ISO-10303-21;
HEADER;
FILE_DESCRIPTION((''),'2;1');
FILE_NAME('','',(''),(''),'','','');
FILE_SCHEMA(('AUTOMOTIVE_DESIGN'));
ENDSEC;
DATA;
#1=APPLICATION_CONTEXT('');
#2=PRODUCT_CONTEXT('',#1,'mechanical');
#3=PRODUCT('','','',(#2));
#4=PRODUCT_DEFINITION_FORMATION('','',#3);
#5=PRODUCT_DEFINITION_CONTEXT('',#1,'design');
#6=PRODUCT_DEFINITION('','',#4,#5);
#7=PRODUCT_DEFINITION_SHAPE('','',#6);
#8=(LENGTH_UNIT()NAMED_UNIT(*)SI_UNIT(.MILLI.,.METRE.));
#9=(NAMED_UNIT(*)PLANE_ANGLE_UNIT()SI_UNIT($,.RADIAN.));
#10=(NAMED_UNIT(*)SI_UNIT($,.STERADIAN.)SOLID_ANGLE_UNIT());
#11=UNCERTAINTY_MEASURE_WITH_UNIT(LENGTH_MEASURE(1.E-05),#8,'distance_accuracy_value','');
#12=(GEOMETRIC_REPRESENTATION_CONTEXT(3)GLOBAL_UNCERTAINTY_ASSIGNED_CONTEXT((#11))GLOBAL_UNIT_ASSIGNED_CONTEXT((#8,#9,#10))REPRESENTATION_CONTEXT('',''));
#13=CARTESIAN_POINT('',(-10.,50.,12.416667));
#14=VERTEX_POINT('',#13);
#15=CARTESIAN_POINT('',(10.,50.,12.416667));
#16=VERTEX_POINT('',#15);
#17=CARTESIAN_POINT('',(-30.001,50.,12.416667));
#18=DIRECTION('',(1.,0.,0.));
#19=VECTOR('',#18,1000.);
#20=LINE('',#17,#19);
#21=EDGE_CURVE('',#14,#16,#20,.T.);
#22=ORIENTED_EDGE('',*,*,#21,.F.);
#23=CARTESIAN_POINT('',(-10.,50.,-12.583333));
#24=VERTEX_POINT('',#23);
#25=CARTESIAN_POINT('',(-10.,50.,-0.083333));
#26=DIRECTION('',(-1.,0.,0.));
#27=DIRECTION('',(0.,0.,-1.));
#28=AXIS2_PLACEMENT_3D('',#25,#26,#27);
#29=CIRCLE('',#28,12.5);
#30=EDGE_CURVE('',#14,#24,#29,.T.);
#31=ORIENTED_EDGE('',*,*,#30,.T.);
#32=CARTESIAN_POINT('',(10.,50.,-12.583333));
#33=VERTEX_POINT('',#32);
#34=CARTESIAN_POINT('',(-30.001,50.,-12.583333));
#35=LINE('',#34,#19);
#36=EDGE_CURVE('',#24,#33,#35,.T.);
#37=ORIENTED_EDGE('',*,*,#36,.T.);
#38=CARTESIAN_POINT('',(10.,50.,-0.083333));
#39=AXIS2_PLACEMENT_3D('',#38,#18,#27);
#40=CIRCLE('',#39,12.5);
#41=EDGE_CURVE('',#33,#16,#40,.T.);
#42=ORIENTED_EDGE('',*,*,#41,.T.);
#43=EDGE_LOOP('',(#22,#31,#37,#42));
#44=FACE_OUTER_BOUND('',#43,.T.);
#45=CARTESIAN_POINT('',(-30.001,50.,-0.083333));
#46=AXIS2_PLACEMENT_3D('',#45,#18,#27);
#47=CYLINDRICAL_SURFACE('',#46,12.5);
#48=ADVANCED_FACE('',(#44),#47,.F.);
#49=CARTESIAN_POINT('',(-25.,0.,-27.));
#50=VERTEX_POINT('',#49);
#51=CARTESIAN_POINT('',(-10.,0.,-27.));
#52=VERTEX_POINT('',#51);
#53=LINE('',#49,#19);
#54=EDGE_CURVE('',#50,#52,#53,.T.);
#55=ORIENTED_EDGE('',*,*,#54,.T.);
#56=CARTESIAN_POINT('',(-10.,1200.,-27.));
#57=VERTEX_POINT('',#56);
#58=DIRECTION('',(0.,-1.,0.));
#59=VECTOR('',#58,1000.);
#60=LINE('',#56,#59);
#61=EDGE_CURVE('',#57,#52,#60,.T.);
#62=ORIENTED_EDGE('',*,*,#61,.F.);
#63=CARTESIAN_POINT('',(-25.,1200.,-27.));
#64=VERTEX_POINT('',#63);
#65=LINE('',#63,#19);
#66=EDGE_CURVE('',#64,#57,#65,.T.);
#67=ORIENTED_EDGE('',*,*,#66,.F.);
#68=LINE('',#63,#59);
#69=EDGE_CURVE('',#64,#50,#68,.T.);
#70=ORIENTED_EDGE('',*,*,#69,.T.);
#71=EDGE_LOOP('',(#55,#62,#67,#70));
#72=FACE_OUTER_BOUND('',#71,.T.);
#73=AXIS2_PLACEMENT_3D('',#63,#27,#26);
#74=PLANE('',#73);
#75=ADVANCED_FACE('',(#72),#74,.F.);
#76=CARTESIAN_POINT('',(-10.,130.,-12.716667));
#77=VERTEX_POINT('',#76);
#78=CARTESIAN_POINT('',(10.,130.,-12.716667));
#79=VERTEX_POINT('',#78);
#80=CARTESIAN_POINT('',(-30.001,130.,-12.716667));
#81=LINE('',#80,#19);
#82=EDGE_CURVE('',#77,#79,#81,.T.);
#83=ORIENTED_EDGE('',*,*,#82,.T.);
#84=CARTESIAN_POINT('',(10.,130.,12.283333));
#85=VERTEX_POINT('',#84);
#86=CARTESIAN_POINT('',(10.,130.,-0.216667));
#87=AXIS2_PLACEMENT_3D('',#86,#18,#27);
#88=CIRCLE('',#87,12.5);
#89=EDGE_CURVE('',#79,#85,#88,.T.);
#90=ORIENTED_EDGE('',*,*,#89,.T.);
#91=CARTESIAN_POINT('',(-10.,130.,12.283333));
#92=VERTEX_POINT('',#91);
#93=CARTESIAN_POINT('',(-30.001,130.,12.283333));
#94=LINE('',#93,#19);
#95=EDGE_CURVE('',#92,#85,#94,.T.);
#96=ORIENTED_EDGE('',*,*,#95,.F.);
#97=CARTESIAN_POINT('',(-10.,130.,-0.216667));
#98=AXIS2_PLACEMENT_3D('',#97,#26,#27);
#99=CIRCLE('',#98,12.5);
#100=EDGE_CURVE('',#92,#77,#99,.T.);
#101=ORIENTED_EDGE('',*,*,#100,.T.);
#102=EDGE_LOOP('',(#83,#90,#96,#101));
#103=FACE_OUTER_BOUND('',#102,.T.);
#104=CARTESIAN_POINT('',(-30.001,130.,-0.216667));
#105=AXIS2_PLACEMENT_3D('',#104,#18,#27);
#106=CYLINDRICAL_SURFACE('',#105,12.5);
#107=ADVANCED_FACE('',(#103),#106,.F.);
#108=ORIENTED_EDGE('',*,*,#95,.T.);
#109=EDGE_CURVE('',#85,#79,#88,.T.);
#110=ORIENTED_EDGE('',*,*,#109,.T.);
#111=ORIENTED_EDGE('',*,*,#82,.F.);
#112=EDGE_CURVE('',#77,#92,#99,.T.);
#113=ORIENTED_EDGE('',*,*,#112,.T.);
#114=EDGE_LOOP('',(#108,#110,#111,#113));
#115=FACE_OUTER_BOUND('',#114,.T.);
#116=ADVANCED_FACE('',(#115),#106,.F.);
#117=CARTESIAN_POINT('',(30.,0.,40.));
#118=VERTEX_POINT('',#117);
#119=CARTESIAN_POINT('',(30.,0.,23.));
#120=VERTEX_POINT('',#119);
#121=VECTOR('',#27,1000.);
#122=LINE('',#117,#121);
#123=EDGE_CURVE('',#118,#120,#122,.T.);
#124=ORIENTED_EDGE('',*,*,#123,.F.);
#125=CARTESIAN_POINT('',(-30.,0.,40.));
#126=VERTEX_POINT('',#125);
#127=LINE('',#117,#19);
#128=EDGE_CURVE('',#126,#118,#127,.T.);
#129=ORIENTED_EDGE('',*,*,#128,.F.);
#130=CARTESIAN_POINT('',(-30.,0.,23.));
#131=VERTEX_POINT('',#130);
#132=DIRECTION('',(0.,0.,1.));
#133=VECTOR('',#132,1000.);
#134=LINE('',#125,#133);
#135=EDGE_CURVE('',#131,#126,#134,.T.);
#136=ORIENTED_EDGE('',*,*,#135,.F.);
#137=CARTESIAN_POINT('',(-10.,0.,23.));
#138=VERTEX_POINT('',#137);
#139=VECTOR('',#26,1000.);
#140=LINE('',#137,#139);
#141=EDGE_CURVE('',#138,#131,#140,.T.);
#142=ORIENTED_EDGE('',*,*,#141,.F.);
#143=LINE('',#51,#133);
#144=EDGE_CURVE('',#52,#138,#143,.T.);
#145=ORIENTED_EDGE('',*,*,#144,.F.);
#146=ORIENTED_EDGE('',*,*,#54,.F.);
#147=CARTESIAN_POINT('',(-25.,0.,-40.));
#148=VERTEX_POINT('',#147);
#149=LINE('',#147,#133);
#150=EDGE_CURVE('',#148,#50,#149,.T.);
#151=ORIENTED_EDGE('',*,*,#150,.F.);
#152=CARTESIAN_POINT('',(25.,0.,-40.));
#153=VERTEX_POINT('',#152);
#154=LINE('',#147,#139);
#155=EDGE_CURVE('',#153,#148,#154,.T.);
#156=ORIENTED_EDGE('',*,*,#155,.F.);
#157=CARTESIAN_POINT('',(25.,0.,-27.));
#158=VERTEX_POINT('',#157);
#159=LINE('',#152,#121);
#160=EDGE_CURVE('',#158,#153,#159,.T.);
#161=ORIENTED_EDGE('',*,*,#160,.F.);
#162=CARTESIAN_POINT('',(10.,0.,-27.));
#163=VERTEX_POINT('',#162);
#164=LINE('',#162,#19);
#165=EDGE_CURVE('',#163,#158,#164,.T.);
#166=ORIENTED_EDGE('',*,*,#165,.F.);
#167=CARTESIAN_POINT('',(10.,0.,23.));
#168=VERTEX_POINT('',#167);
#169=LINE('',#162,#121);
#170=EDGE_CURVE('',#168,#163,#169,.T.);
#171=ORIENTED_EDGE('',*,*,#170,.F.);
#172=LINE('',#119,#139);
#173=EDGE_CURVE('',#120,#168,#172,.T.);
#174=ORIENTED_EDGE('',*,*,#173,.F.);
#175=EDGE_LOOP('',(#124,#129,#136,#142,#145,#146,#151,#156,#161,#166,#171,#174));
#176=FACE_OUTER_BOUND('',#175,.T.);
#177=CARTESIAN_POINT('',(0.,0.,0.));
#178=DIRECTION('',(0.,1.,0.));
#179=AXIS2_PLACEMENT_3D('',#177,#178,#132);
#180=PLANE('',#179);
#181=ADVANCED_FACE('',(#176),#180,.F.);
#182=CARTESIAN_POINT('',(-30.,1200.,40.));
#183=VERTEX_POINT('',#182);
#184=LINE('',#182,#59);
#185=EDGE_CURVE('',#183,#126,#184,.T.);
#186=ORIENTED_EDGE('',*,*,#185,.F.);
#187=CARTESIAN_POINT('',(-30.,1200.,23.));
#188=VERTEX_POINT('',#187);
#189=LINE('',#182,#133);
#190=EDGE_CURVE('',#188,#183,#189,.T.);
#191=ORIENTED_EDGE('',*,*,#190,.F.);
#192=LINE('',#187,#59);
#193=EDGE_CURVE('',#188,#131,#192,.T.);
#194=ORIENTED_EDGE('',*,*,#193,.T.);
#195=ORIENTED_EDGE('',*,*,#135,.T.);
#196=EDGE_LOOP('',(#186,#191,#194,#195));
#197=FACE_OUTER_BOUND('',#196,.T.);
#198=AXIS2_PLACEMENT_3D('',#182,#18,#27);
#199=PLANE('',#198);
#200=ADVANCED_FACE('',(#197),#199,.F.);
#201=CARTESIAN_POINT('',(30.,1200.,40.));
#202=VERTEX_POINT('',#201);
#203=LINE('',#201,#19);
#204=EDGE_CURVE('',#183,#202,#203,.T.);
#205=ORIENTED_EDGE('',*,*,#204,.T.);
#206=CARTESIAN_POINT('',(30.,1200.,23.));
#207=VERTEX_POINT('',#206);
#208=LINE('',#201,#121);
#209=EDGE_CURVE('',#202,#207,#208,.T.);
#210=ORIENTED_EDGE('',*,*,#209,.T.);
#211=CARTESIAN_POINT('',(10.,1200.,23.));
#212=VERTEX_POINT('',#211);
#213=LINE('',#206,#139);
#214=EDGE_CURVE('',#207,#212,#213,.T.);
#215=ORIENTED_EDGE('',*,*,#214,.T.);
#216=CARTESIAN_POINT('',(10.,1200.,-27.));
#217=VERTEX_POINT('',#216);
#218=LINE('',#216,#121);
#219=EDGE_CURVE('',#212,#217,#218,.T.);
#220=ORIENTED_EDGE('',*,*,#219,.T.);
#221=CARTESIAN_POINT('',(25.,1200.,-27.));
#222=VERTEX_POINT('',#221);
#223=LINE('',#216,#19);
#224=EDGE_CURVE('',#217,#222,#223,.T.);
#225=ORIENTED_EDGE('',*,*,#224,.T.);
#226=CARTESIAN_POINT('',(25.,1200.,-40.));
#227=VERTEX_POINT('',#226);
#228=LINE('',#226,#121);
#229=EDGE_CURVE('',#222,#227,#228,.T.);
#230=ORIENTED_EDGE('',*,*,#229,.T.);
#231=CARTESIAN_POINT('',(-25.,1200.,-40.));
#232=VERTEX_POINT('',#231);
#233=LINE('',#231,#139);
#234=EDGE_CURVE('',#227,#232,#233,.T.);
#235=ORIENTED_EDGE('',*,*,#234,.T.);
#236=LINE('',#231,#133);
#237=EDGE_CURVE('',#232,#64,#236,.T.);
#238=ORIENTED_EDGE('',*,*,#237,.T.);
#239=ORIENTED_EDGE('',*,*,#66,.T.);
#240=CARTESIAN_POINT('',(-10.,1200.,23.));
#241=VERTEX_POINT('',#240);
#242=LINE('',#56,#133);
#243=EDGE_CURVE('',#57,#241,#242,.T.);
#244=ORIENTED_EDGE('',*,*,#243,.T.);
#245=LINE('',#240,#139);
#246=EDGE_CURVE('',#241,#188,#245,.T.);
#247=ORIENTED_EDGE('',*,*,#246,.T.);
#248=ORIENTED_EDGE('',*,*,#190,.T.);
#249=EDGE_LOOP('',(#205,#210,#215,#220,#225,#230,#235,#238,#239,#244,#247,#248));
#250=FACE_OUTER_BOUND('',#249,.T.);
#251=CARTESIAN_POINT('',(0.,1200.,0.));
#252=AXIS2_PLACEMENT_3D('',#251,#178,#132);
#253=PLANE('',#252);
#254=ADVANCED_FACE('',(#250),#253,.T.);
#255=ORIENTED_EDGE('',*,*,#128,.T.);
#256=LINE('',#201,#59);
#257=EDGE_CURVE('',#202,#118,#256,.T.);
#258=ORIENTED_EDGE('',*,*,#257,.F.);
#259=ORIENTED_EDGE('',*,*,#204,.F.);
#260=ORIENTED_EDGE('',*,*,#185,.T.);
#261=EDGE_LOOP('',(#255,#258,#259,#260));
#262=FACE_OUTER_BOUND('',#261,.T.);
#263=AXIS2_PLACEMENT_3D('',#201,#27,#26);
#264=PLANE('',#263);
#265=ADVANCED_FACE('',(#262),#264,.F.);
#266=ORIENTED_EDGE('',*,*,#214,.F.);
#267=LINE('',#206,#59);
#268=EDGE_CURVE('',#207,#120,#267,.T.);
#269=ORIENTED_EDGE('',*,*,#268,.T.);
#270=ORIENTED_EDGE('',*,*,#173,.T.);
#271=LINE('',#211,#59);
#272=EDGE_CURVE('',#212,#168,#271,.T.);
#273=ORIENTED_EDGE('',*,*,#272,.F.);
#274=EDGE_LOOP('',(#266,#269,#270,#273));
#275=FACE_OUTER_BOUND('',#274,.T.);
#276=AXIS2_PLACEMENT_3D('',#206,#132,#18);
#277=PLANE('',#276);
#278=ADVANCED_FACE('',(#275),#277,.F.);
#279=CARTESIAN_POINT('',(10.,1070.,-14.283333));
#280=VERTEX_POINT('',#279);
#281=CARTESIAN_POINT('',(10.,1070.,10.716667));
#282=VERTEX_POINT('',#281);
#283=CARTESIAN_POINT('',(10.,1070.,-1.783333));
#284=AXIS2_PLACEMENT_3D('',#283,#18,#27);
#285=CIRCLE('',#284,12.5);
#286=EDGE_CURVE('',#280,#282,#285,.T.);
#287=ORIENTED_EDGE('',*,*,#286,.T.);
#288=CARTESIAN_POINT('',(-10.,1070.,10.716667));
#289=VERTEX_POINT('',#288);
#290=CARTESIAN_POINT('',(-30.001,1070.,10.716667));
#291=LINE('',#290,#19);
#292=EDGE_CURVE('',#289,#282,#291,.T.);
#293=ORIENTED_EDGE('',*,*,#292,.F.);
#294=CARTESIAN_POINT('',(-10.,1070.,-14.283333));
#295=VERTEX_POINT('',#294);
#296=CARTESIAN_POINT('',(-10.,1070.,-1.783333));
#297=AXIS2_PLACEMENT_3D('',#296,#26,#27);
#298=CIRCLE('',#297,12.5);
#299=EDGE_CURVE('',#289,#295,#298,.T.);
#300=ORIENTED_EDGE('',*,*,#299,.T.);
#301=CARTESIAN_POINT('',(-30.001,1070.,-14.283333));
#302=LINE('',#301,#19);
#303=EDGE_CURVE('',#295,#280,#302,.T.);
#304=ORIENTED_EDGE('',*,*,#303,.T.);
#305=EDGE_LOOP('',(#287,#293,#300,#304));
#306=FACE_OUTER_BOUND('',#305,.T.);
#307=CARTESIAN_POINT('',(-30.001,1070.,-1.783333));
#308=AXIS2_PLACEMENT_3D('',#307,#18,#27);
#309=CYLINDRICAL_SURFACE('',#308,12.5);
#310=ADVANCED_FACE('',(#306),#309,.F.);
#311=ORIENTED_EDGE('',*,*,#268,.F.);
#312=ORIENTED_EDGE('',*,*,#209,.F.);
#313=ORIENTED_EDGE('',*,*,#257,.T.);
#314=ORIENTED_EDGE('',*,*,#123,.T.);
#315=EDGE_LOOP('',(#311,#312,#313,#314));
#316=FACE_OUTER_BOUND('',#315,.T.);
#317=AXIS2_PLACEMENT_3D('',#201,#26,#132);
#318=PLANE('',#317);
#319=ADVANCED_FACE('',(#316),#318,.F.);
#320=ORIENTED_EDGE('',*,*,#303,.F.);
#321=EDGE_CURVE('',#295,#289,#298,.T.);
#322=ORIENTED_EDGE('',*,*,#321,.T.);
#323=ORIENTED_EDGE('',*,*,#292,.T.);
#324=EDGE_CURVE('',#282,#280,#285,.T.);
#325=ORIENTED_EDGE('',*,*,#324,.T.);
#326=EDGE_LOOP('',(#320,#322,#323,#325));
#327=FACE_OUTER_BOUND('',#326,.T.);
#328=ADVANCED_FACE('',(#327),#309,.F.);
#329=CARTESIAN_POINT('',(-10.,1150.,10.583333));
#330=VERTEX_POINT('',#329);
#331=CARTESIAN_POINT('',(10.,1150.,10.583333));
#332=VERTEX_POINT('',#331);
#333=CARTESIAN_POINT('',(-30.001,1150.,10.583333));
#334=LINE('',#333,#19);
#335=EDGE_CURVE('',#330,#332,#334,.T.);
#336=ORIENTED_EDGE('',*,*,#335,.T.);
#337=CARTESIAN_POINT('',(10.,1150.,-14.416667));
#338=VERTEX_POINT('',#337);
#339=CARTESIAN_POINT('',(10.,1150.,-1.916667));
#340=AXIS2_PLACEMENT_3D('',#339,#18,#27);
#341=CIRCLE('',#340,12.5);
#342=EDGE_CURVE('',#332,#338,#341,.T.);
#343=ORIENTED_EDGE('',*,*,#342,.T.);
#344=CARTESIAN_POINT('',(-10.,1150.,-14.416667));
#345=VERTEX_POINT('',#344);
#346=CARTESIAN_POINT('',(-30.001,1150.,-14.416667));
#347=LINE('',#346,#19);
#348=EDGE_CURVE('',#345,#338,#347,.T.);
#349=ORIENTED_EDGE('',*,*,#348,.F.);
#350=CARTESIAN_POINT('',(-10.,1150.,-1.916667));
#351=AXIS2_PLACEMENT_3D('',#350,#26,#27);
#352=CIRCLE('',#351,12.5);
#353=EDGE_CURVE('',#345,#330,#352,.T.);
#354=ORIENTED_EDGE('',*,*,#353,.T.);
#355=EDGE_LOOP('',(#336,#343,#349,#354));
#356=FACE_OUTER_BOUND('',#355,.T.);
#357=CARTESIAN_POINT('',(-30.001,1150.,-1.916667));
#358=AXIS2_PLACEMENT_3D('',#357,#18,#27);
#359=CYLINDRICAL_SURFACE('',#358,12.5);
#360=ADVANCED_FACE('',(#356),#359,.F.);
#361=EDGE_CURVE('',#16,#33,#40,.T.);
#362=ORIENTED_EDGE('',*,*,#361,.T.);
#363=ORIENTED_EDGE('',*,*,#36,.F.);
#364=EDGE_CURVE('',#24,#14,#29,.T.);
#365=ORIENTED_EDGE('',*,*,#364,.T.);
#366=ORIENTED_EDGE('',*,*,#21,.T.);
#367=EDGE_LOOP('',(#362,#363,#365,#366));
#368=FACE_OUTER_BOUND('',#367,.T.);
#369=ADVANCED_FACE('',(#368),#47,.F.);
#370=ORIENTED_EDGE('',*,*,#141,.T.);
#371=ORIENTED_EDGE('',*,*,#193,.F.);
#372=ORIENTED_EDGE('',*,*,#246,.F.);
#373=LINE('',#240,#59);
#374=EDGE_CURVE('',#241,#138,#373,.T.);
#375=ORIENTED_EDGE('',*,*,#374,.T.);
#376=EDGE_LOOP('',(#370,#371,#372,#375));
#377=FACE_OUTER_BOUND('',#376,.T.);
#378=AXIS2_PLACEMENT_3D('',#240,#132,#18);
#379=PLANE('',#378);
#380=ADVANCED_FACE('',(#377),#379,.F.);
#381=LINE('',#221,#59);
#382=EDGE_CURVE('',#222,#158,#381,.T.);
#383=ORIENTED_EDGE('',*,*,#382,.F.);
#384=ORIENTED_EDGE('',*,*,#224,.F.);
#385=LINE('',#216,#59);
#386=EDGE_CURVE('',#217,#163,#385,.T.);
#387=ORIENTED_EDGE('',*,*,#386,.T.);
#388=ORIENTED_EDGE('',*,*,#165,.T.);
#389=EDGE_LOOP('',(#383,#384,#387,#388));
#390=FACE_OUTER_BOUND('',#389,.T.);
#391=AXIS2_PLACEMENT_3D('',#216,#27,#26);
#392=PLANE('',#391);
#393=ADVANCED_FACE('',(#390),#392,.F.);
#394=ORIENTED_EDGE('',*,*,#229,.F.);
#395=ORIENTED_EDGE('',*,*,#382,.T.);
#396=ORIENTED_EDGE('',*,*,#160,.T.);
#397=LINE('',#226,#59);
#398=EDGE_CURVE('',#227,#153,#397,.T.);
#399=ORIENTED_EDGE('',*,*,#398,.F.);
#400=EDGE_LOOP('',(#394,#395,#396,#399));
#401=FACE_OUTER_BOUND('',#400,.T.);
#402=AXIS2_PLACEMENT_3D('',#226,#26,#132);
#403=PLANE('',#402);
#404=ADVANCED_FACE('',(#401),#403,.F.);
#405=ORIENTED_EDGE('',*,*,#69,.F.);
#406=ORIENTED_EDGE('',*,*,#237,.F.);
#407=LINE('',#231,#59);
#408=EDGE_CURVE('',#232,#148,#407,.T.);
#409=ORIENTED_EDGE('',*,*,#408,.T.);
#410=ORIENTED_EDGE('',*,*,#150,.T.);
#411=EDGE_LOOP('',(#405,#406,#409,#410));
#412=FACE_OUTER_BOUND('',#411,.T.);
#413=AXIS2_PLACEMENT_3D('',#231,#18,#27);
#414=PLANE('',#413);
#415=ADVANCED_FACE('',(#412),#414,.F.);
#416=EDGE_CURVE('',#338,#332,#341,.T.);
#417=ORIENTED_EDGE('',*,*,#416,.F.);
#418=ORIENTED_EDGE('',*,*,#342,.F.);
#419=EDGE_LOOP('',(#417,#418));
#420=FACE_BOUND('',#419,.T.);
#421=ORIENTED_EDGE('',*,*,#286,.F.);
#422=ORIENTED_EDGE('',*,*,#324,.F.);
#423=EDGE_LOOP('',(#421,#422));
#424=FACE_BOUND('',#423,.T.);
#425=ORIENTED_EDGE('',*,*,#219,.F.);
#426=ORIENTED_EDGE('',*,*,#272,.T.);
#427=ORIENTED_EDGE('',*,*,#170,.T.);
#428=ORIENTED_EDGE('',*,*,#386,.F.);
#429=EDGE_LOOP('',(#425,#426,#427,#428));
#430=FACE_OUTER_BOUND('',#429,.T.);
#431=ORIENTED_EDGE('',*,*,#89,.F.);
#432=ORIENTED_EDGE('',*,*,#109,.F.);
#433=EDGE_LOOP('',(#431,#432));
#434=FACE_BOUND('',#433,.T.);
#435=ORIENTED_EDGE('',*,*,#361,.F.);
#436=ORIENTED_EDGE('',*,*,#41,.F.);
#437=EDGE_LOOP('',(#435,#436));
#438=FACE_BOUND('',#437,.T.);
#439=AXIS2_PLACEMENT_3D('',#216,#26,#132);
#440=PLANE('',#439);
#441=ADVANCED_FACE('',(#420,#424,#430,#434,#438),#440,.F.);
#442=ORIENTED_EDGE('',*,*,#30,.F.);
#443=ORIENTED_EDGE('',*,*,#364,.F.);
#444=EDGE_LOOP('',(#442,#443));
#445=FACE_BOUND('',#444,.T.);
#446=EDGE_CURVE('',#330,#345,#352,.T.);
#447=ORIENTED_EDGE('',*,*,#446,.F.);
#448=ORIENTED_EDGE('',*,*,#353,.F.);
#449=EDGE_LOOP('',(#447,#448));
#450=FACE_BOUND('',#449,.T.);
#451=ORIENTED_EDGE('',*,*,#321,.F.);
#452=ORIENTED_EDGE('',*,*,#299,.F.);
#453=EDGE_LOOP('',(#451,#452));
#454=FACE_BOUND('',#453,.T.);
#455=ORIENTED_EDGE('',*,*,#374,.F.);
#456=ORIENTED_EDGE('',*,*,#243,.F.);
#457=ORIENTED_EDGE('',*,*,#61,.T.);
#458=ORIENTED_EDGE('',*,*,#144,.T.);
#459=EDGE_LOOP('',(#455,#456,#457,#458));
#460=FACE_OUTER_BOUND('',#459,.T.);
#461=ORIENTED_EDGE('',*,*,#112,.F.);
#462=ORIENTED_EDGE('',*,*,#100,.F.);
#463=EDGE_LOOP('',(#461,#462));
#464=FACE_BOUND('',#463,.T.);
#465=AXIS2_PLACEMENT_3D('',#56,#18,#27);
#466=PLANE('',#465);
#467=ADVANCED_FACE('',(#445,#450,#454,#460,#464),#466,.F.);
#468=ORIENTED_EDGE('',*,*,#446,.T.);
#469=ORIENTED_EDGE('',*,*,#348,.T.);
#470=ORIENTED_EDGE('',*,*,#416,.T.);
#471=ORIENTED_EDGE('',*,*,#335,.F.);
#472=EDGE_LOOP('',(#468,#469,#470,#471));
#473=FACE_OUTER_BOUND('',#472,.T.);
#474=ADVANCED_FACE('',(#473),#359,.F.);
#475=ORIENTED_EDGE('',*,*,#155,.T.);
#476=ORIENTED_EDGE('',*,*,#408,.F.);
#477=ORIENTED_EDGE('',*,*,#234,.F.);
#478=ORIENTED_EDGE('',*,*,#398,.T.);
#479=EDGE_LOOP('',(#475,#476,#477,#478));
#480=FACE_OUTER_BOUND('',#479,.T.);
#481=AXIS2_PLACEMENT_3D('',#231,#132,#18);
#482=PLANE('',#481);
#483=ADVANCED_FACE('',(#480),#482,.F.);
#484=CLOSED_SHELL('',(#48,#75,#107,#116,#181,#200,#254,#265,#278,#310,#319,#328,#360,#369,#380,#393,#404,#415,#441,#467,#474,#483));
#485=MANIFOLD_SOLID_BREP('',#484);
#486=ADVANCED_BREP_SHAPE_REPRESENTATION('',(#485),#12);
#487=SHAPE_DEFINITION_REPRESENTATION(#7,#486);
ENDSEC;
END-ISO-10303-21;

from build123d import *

# Parameters (mm, degrees)
BOSS_EXTRUDE1_DEPTH = 1200
CUT_EXTRUDE1_REACH  = 1203.333
SKETCH2_R           = 12.5


with BuildPart() as part:
    # Sketch1 → Boss-Extrude1 (new body)
    with BuildSketch(Plane(origin=(0, 0, 0), x_dir=(1, 0, 0), z_dir=(0, 1, 0))):
        Polygon((10, 27), (25, 27), (25, 40), (-25, 40), (-25, 27), (-10, 27), (-10, -23), (-30, -23), (-30, -40), (30, -40), (30, -23), (10, -23), align=None)
    extrude(amount=BOSS_EXTRUDE1_DEPTH)

    # Sketch2 → Cut-Extrude1 (cut, up to next)
    with BuildSketch(Plane(origin=(10, 0, 0), x_dir=(0, 0, -1), z_dir=(1, 0, 0)), mode=Mode.PRIVATE) as cut_extrude1_sk1:
        with Locations((1.916666667, 1150)):
            Circle(SKETCH2_R)
    cut_extrude1_tool1 = extrude(cut_extrude1_sk1.sketch, amount=-CUT_EXTRUDE1_REACH, mode=Mode.PRIVATE) & part.part
    # Sketch2 → Cut-Extrude1 (cut, up to next)
    with BuildSketch(Plane(origin=(10, 0, 0), x_dir=(0, 0, -1), z_dir=(1, 0, 0)), mode=Mode.PRIVATE) as cut_extrude1_sk2:
        with Locations((1.783333333, 1070)):
            Circle(SKETCH2_R)
    cut_extrude1_tool2 = extrude(cut_extrude1_sk2.sketch, amount=-CUT_EXTRUDE1_REACH, mode=Mode.PRIVATE) & part.part
    # Sketch2 → Cut-Extrude1 (cut, up to next)
    with BuildSketch(Plane(origin=(10, 0, 0), x_dir=(0, 0, -1), z_dir=(1, 0, 0)), mode=Mode.PRIVATE) as cut_extrude1_sk3:
        with Locations((0.083333333, 50)):
            Circle(SKETCH2_R)
    cut_extrude1_tool3 = extrude(cut_extrude1_sk3.sketch, amount=-CUT_EXTRUDE1_REACH, mode=Mode.PRIVATE) & part.part
    # Sketch2 → Cut-Extrude1 (cut, up to next)
    with BuildSketch(Plane(origin=(10, 0, 0), x_dir=(0, 0, -1), z_dir=(1, 0, 0)), mode=Mode.PRIVATE) as cut_extrude1_sk4:
        with Locations((0.216666667, 130)):
            Circle(SKETCH2_R)
    cut_extrude1_tool4 = extrude(cut_extrude1_sk4.sketch, amount=-CUT_EXTRUDE1_REACH, mode=Mode.PRIVATE) & part.part
    add(cut_extrude1_tool1.solids().sort_by_distance((10, 1150, -1.916667))[0], mode=Mode.SUBTRACT)
    add(cut_extrude1_tool2.solids().sort_by_distance((10, 1070, -1.783333))[0], mode=Mode.SUBTRACT)
    add(cut_extrude1_tool3.solids().sort_by_distance((10, 50, -0.083333))[0], mode=Mode.SUBTRACT)
    add(cut_extrude1_tool4.solids().sort_by_distance((10, 130, -0.216667))[0], mode=Mode.SUBTRACT)


solid = part.part
